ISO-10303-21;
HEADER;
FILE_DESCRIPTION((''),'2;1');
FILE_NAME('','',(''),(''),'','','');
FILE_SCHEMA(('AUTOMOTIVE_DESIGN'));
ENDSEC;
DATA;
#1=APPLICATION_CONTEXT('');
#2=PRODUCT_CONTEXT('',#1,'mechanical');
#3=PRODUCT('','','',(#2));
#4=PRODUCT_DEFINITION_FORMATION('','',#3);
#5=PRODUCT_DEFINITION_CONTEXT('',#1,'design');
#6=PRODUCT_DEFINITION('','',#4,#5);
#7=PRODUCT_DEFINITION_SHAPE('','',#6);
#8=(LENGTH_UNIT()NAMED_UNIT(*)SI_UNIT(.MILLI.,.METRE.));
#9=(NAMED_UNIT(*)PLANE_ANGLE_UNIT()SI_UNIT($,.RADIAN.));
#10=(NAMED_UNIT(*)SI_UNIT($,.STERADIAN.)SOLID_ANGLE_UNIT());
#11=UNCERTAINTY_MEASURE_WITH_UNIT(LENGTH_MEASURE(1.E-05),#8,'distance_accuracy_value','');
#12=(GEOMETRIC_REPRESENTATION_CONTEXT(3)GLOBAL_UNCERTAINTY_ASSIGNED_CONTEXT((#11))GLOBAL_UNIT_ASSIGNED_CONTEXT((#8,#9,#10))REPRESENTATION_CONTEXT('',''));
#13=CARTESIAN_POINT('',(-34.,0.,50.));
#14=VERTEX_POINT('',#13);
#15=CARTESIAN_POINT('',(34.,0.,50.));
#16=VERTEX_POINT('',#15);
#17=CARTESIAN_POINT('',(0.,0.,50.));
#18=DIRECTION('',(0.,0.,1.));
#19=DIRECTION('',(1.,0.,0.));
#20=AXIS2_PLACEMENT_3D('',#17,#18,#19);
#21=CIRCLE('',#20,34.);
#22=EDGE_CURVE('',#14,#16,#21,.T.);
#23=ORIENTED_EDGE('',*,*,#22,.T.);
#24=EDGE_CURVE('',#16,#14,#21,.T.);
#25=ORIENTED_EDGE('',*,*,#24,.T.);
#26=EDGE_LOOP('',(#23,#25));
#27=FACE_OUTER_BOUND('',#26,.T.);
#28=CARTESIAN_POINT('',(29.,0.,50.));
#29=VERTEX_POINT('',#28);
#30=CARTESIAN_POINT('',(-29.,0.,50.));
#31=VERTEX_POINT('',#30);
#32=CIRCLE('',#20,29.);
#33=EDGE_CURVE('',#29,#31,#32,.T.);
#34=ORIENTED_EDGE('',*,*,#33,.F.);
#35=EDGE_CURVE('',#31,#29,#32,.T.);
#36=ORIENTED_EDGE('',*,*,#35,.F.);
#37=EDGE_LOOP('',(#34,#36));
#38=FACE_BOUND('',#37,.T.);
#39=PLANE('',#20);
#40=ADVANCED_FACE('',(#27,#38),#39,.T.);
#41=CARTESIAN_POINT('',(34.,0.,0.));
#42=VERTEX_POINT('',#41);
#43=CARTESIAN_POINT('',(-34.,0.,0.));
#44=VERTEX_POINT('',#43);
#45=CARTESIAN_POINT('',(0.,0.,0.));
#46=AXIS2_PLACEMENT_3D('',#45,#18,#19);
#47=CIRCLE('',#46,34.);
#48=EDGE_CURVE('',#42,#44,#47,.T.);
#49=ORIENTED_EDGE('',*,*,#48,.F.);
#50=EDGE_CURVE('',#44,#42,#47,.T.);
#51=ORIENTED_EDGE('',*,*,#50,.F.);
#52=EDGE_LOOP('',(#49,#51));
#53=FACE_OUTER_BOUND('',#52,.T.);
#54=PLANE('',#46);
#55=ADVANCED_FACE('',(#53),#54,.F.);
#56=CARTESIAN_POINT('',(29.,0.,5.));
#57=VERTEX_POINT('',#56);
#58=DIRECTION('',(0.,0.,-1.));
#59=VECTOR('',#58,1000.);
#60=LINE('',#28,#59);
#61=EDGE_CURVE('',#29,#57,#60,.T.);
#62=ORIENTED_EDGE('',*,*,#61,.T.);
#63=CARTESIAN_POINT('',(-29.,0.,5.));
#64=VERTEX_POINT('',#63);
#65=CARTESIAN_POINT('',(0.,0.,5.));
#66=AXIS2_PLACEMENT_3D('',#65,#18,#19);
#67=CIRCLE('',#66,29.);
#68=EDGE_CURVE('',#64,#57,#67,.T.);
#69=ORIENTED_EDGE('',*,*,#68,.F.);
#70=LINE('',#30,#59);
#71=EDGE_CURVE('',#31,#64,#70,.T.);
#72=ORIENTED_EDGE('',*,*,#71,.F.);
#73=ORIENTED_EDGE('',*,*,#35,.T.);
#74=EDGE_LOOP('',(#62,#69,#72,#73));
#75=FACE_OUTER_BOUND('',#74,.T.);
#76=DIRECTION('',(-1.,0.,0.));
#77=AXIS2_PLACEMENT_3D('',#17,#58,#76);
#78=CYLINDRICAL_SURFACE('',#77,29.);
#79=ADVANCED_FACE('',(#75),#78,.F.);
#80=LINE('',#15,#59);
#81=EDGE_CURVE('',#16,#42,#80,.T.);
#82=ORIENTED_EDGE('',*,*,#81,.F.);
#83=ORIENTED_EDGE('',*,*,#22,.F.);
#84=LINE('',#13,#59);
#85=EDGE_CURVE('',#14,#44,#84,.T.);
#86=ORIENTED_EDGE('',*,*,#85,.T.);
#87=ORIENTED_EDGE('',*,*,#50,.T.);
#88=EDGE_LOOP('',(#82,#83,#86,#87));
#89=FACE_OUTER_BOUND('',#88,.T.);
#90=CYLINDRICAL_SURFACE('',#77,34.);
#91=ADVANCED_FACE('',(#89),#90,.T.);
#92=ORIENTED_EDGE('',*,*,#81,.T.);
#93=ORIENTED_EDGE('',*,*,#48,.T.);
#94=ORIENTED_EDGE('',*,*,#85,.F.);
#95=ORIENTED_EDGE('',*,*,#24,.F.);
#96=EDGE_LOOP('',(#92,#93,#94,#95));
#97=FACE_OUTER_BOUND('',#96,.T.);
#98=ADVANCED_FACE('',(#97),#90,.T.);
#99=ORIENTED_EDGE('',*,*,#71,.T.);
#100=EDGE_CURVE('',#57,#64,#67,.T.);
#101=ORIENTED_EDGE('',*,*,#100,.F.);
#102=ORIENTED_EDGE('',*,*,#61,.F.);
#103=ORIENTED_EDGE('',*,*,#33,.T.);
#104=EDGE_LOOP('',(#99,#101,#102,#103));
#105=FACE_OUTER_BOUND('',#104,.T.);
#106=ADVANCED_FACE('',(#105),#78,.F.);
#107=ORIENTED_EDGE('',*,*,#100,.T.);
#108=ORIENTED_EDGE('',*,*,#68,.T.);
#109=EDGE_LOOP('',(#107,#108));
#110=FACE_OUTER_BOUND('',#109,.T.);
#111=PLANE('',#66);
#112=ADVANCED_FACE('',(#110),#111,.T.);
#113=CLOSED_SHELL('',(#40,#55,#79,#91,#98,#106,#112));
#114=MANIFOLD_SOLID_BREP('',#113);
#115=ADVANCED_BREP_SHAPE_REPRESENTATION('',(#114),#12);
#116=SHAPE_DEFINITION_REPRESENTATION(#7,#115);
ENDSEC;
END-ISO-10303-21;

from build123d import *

# Parameters (mm, degrees)
SKETCH1_R           = 34
BOSS_EXTRUDE1_DEPTH = 50
SHELL1_T            = -5


with BuildPart() as part:
    # Sketch1 → Boss-Extrude1 (new body)
    with BuildSketch(Plane.XY):
        Circle(SKETCH1_R)
    extrude(amount=BOSS_EXTRUDE1_DEPTH)

    # Shell1
    shell1_openings = [part.faces().sort_by_distance(p)[0] for p in [
        (0, 0, 50),
    ]]
    offset(amount=SHELL1_T, openings=shell1_openings, kind=Kind.INTERSECTION)


solid = part.part
